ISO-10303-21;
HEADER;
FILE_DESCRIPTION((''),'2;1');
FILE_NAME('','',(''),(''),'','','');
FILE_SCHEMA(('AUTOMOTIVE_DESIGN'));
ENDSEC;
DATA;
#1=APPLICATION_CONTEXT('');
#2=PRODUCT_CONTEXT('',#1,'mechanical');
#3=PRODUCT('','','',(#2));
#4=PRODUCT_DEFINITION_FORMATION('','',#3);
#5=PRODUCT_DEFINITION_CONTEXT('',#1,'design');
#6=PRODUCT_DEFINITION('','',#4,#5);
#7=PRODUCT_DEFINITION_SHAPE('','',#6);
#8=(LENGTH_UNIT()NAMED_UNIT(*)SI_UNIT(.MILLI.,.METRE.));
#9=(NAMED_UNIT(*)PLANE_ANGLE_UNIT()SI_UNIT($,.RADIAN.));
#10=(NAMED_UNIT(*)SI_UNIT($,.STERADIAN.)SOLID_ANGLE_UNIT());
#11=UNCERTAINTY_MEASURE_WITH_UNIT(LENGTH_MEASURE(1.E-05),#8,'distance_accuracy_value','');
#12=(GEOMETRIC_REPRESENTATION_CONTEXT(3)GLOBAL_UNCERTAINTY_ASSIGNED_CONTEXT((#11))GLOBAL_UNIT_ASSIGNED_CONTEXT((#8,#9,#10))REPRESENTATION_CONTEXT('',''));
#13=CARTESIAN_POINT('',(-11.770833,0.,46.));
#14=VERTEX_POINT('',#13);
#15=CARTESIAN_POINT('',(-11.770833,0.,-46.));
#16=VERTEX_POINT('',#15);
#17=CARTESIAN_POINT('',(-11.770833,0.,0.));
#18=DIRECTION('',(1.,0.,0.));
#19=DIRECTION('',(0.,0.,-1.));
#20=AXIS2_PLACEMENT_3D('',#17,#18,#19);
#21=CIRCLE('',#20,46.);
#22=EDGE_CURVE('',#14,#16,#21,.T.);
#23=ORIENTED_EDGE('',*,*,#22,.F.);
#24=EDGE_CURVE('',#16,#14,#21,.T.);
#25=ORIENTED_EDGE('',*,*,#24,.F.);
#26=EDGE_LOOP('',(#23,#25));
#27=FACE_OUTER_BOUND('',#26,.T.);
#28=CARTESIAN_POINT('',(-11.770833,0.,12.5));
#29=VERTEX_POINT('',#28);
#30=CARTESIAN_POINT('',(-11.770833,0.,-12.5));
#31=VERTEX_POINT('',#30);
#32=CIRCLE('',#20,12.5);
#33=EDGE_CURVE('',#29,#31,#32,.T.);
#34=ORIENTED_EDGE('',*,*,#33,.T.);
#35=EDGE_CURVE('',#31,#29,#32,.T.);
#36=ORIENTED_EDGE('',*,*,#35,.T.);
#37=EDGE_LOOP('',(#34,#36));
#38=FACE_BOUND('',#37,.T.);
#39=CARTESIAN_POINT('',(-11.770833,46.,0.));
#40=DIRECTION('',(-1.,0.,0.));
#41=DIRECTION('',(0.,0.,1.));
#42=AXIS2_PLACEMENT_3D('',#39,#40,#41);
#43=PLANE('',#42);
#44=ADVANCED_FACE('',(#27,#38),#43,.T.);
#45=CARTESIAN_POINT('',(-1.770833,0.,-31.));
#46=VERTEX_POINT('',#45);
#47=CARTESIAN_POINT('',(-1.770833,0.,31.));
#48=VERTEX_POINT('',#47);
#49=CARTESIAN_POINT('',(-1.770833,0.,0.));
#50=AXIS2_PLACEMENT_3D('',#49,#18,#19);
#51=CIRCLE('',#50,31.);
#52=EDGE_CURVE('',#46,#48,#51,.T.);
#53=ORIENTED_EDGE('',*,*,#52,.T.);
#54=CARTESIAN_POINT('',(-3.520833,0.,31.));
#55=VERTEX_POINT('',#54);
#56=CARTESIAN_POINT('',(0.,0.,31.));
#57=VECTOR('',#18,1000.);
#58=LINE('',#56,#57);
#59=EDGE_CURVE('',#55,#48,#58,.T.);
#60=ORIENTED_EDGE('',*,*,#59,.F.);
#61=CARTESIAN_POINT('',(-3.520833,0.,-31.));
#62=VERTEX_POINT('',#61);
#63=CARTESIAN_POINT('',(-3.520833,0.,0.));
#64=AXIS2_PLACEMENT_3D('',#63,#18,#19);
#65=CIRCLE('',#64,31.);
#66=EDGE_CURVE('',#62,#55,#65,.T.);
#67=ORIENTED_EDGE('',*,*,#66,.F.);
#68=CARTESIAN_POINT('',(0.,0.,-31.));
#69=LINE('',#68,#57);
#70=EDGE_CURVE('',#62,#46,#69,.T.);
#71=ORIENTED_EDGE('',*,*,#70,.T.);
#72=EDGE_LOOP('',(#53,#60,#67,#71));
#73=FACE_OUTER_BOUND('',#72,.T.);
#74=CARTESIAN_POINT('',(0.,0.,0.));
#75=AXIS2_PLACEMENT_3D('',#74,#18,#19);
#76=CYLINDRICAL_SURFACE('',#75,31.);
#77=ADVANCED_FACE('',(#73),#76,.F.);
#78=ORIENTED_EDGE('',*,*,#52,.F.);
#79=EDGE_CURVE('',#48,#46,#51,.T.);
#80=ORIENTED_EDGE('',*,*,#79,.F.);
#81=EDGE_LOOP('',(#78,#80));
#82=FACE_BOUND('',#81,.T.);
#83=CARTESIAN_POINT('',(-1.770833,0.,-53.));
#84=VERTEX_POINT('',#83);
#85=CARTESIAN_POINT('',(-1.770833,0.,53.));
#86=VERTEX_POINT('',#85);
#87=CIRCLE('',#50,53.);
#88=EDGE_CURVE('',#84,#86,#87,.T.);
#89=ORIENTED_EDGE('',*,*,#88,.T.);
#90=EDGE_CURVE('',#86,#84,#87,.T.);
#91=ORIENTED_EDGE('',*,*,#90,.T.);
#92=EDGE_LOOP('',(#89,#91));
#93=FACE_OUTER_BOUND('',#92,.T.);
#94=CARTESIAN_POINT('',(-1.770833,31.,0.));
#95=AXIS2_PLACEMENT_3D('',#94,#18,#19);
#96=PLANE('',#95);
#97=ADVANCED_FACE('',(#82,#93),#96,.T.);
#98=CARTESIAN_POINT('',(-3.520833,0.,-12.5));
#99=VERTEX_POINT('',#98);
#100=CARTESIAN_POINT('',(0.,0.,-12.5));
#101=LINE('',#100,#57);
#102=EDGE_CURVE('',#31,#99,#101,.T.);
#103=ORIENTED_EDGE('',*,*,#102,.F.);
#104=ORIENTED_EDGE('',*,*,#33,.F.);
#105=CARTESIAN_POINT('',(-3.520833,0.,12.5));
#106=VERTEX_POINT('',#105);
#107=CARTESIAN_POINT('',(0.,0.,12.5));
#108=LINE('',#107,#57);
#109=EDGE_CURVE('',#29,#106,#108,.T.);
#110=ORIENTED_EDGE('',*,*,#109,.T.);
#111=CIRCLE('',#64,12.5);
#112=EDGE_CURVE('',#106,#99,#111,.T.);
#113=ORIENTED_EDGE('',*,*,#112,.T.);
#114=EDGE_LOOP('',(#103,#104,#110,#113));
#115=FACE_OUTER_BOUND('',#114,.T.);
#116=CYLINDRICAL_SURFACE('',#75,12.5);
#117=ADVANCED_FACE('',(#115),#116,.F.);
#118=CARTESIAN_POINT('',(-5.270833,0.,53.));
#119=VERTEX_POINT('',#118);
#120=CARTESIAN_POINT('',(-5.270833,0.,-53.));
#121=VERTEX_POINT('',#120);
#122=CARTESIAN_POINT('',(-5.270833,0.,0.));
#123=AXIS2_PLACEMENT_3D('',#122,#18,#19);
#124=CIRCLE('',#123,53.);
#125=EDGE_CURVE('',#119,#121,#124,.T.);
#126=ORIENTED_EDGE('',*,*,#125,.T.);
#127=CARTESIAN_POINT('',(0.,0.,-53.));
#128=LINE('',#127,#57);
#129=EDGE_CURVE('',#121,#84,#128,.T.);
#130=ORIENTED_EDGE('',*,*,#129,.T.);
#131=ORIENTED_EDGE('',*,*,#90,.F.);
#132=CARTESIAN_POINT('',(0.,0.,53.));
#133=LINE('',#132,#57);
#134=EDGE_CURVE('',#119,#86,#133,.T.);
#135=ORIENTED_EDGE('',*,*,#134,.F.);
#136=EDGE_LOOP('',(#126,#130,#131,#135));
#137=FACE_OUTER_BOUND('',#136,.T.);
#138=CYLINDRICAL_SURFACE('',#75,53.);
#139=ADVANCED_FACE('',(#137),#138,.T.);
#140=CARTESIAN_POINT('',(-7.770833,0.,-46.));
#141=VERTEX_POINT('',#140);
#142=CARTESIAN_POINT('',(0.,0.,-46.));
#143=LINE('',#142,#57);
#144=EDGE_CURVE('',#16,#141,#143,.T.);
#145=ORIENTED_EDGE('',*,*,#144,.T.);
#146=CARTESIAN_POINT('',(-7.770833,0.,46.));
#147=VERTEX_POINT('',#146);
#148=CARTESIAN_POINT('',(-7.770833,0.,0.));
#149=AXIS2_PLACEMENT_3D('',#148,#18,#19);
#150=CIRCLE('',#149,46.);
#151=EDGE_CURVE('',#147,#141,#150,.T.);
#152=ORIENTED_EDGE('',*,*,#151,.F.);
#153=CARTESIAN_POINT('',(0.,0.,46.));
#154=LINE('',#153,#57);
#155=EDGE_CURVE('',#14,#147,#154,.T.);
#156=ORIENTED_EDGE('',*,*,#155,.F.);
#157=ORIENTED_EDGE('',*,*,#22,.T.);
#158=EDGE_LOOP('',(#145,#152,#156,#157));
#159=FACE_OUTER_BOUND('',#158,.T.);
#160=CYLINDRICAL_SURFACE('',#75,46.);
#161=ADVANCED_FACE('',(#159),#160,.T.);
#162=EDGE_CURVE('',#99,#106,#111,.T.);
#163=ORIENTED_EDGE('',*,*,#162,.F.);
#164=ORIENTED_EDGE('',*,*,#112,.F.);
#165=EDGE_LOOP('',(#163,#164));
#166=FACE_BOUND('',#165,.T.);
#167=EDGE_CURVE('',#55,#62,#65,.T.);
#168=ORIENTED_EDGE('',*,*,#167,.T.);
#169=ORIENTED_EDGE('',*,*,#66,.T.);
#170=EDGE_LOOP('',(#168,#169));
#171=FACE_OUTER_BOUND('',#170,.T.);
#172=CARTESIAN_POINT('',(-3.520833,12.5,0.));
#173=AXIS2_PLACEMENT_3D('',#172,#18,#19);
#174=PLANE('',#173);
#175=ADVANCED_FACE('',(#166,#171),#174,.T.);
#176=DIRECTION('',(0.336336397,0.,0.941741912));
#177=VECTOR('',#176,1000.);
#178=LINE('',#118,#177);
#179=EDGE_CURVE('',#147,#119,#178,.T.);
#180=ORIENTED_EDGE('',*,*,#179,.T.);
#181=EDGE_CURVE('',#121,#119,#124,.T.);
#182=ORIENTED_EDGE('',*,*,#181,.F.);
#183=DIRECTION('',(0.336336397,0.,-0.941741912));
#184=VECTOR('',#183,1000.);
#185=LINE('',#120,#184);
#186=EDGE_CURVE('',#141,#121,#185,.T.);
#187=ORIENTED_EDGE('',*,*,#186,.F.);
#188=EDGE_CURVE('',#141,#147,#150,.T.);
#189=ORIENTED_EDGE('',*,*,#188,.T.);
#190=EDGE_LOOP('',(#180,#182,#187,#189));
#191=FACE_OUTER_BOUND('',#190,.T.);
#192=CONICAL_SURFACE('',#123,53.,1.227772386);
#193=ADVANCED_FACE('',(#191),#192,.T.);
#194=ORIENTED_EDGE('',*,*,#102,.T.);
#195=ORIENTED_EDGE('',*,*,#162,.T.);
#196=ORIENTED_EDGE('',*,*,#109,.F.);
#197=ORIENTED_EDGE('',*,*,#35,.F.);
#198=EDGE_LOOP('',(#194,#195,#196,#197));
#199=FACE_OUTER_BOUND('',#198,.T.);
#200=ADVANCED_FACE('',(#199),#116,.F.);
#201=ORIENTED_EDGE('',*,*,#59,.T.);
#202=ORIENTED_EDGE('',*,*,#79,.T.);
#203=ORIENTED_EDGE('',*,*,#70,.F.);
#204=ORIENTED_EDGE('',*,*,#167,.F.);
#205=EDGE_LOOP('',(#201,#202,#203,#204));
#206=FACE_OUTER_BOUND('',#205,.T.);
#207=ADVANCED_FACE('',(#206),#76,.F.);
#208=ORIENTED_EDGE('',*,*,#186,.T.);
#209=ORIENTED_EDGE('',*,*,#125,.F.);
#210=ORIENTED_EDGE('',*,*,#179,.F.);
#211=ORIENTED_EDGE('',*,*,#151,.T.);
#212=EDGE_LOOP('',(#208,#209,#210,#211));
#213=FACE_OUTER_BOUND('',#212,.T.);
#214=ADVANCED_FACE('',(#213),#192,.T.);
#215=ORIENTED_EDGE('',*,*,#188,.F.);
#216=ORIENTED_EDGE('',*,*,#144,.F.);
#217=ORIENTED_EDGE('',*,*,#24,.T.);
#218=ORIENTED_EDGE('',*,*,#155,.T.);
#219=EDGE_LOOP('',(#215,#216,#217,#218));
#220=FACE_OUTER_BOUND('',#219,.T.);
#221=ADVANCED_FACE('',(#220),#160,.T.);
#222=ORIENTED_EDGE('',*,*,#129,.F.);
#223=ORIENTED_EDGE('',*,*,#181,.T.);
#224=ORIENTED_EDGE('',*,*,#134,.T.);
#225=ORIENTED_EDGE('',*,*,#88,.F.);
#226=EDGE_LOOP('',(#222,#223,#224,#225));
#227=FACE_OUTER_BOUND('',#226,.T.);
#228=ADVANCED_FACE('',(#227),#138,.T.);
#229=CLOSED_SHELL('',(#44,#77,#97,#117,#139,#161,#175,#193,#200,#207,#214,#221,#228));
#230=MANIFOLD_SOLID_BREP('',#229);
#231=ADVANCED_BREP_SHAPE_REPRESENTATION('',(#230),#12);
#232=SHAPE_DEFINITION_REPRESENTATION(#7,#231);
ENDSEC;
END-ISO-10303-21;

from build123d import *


with BuildPart() as part:
    # Sketch1 → Revolve1 (revolve)
    with BuildSketch(Plane.XY, mode=Mode.PRIVATE) as revolve1_sk:
        Polygon((-11.770833333, 46), (-11.770833333, 12.5), (-3.520833333, 12.5), (-3.520833333, 31), (-1.770833333, 31), (-1.770833333, 53), (-5.270833333, 53), (-7.770833333, 46), align=None)
    revolve(revolve1_sk.sketch.rotate(Axis((0, 0, 0), (-1, 0, 0)), 90), axis=Axis((0, 0, 0), (-1, 0, 0)))


solid = part.part
